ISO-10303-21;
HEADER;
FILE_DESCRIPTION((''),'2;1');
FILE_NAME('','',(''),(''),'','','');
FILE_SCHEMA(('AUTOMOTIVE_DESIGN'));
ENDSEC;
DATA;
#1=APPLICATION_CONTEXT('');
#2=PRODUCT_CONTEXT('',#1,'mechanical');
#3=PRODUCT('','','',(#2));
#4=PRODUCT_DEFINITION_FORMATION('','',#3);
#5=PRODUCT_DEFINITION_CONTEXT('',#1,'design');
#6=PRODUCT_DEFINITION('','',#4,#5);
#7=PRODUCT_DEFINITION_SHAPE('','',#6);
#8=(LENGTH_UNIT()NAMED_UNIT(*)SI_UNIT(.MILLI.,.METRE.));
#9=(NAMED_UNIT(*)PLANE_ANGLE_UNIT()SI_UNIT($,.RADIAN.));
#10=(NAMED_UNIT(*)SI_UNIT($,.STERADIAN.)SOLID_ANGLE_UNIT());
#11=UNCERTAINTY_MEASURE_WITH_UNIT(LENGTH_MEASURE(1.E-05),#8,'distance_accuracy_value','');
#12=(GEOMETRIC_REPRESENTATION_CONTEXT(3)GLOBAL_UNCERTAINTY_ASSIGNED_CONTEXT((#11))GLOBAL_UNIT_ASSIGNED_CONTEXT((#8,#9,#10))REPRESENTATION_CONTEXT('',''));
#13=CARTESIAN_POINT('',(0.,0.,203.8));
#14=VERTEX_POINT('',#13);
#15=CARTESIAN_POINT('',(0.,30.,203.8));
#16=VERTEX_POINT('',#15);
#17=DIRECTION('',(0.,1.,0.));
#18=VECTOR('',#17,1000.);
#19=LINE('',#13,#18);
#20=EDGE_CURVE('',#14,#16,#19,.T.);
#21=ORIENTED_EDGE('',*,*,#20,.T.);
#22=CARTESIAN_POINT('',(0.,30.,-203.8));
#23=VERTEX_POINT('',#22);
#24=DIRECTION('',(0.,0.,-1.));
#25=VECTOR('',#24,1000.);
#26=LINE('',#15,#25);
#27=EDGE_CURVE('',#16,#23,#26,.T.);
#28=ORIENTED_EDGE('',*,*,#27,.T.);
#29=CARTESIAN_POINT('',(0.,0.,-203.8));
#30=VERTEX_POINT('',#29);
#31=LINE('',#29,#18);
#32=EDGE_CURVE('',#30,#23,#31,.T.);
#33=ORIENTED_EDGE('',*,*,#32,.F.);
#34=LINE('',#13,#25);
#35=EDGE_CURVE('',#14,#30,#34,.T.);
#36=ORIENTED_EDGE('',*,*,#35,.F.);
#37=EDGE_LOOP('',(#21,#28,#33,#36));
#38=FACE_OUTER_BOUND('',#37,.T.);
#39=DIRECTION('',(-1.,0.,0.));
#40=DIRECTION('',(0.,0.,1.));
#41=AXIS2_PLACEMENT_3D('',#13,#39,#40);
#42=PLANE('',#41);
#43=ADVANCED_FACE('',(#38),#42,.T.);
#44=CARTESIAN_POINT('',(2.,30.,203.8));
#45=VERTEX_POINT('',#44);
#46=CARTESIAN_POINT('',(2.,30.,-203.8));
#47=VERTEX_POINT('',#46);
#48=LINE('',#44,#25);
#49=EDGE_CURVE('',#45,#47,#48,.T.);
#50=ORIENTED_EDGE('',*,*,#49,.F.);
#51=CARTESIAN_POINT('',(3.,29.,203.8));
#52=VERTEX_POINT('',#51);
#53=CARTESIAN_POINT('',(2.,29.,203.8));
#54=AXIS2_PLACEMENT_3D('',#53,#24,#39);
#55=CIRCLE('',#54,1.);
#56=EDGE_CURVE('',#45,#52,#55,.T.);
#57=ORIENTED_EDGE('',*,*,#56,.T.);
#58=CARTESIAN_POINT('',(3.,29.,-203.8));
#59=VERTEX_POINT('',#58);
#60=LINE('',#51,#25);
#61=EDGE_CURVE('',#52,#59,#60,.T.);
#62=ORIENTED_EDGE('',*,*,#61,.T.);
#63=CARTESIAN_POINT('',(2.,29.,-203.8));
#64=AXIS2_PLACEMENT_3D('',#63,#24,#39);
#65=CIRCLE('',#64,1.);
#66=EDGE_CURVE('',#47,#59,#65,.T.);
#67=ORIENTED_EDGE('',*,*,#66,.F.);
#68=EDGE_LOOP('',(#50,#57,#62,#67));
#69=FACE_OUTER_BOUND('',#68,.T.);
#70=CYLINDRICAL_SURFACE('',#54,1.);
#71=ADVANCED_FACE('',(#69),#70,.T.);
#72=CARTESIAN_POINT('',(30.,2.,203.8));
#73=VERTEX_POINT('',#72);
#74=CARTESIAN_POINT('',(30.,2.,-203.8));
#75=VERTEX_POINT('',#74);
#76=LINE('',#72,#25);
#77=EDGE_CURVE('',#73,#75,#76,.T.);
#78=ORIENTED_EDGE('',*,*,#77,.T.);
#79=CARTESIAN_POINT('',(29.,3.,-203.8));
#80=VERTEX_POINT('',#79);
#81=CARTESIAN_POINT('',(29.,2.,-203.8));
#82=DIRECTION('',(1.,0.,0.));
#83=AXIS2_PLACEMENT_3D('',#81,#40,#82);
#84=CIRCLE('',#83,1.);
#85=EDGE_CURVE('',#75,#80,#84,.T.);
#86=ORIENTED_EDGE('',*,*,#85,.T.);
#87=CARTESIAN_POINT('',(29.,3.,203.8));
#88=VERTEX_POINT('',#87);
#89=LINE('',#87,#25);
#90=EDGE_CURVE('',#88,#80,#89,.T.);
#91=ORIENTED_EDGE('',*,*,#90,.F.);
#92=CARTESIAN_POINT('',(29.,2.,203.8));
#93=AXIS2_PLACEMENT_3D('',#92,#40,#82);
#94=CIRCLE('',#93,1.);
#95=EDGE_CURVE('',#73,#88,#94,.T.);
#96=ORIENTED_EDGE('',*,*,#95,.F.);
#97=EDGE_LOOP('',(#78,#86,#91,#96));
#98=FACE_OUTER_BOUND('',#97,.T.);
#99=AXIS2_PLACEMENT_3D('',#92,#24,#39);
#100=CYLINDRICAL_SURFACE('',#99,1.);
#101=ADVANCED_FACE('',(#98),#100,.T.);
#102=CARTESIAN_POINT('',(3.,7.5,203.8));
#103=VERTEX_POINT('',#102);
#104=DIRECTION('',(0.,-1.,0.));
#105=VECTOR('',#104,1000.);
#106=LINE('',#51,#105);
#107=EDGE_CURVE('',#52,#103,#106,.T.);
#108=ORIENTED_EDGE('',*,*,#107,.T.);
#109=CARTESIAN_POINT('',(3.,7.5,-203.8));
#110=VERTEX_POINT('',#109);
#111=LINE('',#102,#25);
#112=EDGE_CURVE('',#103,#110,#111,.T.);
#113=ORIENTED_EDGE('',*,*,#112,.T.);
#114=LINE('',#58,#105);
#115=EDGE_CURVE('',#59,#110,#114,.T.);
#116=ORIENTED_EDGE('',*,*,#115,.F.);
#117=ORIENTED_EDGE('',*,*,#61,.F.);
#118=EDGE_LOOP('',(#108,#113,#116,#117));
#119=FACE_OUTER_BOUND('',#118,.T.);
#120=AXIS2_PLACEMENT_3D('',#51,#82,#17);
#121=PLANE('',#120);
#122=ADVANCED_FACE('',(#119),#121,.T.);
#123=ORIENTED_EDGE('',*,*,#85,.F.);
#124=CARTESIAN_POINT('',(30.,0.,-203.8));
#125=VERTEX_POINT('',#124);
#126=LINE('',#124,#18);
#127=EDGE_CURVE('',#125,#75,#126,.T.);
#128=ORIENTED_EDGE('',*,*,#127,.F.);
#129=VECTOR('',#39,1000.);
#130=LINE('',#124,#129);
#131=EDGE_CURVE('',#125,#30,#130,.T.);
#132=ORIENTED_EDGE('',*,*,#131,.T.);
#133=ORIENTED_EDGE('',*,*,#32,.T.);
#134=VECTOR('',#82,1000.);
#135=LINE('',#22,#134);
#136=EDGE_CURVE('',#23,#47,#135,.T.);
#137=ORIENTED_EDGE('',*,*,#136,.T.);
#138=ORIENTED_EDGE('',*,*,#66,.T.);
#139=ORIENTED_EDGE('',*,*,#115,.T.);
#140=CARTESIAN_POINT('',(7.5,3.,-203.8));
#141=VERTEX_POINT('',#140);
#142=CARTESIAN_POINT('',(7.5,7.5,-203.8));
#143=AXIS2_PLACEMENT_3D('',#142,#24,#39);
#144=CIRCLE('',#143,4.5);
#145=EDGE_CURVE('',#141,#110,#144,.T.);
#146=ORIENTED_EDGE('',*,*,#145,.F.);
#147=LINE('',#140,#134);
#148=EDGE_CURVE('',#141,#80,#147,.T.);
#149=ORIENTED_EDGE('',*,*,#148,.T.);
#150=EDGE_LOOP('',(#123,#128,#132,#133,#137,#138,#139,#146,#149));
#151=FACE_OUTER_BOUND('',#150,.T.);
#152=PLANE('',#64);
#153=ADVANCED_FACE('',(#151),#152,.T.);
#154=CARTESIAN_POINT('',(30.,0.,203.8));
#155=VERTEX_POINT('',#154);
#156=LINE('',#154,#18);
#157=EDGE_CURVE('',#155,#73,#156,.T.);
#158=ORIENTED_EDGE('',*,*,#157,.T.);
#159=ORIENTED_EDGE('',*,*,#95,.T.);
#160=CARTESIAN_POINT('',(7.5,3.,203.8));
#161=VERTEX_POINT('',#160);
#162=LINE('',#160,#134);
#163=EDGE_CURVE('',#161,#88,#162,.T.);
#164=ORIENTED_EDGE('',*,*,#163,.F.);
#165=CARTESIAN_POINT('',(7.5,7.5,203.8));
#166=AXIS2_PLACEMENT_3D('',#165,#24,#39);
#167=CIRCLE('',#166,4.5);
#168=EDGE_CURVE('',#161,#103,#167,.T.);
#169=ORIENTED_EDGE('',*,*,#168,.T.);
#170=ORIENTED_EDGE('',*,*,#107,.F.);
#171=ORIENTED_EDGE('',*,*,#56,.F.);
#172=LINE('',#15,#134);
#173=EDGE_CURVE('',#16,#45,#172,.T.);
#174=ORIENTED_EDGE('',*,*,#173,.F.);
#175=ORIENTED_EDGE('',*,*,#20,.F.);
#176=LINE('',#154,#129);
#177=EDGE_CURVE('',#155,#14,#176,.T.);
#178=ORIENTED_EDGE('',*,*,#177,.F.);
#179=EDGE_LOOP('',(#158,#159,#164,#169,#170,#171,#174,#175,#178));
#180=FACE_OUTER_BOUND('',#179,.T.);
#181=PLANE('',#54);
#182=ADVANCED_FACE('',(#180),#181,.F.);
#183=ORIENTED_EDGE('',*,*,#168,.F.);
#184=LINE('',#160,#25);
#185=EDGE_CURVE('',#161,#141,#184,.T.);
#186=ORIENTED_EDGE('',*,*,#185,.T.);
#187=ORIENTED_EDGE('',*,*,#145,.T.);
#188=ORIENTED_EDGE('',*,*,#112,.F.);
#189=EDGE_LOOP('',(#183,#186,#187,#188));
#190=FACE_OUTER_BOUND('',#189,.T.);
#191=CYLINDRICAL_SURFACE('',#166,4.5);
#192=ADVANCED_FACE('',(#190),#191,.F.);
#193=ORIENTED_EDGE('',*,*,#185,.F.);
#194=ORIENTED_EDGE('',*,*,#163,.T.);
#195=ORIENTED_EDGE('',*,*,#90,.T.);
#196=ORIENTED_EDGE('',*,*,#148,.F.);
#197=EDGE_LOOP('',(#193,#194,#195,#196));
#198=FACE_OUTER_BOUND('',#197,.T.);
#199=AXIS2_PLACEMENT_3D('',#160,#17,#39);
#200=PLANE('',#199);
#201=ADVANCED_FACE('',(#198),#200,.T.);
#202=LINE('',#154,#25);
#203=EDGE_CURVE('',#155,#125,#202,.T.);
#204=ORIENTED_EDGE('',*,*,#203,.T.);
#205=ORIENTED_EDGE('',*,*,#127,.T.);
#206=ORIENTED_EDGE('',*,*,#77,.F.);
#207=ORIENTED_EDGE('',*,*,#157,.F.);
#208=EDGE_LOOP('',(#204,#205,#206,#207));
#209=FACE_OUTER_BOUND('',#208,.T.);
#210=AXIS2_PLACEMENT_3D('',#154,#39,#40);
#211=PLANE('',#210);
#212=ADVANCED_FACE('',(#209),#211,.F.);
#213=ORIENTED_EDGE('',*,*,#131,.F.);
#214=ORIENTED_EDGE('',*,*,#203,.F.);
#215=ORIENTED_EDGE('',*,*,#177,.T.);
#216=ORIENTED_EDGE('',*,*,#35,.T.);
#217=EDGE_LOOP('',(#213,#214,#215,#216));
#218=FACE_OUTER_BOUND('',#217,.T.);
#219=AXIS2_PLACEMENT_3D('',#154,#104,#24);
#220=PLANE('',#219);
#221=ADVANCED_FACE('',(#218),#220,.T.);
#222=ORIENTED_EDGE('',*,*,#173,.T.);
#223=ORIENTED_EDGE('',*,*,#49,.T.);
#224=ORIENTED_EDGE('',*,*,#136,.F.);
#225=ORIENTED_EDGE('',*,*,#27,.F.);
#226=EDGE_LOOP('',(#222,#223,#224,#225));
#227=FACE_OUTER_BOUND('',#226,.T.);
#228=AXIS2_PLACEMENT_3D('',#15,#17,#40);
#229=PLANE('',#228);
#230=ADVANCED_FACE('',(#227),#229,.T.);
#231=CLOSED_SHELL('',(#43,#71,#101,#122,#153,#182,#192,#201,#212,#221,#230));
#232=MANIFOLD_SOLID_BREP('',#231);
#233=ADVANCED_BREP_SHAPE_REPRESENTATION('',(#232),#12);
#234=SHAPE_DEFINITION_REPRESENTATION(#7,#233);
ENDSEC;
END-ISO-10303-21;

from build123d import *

# Parameters (mm, degrees)
BOSS_EXTRUDE1_DEPTH = 203.8


with BuildPart() as part:
    # Sketch1 → Boss-Extrude1 (new, symmetric)
    with BuildSketch(Plane.XY):
        with BuildLine():
            Line((0, 0), (0, 30))
            Line((0, 30), (2, 30))
            ThreePointArc((2, 30), (2.707106781, 29.707106781), (3, 29))
            Line((3, 29), (3, 7.5))
            ThreePointArc((3, 7.5), (4.318019485, 4.318019485), (7.5, 3))
            Line((7.5, 3), (29, 3))
            ThreePointArc((29, 3), (29.707106781, 2.707106781), (30, 2))
            Line((30, 2), (30, 0))
            Line((30, 0), (0, 0))
        make_face()
    extrude(amount=BOSS_EXTRUDE1_DEPTH, both=True)


solid = part.part
